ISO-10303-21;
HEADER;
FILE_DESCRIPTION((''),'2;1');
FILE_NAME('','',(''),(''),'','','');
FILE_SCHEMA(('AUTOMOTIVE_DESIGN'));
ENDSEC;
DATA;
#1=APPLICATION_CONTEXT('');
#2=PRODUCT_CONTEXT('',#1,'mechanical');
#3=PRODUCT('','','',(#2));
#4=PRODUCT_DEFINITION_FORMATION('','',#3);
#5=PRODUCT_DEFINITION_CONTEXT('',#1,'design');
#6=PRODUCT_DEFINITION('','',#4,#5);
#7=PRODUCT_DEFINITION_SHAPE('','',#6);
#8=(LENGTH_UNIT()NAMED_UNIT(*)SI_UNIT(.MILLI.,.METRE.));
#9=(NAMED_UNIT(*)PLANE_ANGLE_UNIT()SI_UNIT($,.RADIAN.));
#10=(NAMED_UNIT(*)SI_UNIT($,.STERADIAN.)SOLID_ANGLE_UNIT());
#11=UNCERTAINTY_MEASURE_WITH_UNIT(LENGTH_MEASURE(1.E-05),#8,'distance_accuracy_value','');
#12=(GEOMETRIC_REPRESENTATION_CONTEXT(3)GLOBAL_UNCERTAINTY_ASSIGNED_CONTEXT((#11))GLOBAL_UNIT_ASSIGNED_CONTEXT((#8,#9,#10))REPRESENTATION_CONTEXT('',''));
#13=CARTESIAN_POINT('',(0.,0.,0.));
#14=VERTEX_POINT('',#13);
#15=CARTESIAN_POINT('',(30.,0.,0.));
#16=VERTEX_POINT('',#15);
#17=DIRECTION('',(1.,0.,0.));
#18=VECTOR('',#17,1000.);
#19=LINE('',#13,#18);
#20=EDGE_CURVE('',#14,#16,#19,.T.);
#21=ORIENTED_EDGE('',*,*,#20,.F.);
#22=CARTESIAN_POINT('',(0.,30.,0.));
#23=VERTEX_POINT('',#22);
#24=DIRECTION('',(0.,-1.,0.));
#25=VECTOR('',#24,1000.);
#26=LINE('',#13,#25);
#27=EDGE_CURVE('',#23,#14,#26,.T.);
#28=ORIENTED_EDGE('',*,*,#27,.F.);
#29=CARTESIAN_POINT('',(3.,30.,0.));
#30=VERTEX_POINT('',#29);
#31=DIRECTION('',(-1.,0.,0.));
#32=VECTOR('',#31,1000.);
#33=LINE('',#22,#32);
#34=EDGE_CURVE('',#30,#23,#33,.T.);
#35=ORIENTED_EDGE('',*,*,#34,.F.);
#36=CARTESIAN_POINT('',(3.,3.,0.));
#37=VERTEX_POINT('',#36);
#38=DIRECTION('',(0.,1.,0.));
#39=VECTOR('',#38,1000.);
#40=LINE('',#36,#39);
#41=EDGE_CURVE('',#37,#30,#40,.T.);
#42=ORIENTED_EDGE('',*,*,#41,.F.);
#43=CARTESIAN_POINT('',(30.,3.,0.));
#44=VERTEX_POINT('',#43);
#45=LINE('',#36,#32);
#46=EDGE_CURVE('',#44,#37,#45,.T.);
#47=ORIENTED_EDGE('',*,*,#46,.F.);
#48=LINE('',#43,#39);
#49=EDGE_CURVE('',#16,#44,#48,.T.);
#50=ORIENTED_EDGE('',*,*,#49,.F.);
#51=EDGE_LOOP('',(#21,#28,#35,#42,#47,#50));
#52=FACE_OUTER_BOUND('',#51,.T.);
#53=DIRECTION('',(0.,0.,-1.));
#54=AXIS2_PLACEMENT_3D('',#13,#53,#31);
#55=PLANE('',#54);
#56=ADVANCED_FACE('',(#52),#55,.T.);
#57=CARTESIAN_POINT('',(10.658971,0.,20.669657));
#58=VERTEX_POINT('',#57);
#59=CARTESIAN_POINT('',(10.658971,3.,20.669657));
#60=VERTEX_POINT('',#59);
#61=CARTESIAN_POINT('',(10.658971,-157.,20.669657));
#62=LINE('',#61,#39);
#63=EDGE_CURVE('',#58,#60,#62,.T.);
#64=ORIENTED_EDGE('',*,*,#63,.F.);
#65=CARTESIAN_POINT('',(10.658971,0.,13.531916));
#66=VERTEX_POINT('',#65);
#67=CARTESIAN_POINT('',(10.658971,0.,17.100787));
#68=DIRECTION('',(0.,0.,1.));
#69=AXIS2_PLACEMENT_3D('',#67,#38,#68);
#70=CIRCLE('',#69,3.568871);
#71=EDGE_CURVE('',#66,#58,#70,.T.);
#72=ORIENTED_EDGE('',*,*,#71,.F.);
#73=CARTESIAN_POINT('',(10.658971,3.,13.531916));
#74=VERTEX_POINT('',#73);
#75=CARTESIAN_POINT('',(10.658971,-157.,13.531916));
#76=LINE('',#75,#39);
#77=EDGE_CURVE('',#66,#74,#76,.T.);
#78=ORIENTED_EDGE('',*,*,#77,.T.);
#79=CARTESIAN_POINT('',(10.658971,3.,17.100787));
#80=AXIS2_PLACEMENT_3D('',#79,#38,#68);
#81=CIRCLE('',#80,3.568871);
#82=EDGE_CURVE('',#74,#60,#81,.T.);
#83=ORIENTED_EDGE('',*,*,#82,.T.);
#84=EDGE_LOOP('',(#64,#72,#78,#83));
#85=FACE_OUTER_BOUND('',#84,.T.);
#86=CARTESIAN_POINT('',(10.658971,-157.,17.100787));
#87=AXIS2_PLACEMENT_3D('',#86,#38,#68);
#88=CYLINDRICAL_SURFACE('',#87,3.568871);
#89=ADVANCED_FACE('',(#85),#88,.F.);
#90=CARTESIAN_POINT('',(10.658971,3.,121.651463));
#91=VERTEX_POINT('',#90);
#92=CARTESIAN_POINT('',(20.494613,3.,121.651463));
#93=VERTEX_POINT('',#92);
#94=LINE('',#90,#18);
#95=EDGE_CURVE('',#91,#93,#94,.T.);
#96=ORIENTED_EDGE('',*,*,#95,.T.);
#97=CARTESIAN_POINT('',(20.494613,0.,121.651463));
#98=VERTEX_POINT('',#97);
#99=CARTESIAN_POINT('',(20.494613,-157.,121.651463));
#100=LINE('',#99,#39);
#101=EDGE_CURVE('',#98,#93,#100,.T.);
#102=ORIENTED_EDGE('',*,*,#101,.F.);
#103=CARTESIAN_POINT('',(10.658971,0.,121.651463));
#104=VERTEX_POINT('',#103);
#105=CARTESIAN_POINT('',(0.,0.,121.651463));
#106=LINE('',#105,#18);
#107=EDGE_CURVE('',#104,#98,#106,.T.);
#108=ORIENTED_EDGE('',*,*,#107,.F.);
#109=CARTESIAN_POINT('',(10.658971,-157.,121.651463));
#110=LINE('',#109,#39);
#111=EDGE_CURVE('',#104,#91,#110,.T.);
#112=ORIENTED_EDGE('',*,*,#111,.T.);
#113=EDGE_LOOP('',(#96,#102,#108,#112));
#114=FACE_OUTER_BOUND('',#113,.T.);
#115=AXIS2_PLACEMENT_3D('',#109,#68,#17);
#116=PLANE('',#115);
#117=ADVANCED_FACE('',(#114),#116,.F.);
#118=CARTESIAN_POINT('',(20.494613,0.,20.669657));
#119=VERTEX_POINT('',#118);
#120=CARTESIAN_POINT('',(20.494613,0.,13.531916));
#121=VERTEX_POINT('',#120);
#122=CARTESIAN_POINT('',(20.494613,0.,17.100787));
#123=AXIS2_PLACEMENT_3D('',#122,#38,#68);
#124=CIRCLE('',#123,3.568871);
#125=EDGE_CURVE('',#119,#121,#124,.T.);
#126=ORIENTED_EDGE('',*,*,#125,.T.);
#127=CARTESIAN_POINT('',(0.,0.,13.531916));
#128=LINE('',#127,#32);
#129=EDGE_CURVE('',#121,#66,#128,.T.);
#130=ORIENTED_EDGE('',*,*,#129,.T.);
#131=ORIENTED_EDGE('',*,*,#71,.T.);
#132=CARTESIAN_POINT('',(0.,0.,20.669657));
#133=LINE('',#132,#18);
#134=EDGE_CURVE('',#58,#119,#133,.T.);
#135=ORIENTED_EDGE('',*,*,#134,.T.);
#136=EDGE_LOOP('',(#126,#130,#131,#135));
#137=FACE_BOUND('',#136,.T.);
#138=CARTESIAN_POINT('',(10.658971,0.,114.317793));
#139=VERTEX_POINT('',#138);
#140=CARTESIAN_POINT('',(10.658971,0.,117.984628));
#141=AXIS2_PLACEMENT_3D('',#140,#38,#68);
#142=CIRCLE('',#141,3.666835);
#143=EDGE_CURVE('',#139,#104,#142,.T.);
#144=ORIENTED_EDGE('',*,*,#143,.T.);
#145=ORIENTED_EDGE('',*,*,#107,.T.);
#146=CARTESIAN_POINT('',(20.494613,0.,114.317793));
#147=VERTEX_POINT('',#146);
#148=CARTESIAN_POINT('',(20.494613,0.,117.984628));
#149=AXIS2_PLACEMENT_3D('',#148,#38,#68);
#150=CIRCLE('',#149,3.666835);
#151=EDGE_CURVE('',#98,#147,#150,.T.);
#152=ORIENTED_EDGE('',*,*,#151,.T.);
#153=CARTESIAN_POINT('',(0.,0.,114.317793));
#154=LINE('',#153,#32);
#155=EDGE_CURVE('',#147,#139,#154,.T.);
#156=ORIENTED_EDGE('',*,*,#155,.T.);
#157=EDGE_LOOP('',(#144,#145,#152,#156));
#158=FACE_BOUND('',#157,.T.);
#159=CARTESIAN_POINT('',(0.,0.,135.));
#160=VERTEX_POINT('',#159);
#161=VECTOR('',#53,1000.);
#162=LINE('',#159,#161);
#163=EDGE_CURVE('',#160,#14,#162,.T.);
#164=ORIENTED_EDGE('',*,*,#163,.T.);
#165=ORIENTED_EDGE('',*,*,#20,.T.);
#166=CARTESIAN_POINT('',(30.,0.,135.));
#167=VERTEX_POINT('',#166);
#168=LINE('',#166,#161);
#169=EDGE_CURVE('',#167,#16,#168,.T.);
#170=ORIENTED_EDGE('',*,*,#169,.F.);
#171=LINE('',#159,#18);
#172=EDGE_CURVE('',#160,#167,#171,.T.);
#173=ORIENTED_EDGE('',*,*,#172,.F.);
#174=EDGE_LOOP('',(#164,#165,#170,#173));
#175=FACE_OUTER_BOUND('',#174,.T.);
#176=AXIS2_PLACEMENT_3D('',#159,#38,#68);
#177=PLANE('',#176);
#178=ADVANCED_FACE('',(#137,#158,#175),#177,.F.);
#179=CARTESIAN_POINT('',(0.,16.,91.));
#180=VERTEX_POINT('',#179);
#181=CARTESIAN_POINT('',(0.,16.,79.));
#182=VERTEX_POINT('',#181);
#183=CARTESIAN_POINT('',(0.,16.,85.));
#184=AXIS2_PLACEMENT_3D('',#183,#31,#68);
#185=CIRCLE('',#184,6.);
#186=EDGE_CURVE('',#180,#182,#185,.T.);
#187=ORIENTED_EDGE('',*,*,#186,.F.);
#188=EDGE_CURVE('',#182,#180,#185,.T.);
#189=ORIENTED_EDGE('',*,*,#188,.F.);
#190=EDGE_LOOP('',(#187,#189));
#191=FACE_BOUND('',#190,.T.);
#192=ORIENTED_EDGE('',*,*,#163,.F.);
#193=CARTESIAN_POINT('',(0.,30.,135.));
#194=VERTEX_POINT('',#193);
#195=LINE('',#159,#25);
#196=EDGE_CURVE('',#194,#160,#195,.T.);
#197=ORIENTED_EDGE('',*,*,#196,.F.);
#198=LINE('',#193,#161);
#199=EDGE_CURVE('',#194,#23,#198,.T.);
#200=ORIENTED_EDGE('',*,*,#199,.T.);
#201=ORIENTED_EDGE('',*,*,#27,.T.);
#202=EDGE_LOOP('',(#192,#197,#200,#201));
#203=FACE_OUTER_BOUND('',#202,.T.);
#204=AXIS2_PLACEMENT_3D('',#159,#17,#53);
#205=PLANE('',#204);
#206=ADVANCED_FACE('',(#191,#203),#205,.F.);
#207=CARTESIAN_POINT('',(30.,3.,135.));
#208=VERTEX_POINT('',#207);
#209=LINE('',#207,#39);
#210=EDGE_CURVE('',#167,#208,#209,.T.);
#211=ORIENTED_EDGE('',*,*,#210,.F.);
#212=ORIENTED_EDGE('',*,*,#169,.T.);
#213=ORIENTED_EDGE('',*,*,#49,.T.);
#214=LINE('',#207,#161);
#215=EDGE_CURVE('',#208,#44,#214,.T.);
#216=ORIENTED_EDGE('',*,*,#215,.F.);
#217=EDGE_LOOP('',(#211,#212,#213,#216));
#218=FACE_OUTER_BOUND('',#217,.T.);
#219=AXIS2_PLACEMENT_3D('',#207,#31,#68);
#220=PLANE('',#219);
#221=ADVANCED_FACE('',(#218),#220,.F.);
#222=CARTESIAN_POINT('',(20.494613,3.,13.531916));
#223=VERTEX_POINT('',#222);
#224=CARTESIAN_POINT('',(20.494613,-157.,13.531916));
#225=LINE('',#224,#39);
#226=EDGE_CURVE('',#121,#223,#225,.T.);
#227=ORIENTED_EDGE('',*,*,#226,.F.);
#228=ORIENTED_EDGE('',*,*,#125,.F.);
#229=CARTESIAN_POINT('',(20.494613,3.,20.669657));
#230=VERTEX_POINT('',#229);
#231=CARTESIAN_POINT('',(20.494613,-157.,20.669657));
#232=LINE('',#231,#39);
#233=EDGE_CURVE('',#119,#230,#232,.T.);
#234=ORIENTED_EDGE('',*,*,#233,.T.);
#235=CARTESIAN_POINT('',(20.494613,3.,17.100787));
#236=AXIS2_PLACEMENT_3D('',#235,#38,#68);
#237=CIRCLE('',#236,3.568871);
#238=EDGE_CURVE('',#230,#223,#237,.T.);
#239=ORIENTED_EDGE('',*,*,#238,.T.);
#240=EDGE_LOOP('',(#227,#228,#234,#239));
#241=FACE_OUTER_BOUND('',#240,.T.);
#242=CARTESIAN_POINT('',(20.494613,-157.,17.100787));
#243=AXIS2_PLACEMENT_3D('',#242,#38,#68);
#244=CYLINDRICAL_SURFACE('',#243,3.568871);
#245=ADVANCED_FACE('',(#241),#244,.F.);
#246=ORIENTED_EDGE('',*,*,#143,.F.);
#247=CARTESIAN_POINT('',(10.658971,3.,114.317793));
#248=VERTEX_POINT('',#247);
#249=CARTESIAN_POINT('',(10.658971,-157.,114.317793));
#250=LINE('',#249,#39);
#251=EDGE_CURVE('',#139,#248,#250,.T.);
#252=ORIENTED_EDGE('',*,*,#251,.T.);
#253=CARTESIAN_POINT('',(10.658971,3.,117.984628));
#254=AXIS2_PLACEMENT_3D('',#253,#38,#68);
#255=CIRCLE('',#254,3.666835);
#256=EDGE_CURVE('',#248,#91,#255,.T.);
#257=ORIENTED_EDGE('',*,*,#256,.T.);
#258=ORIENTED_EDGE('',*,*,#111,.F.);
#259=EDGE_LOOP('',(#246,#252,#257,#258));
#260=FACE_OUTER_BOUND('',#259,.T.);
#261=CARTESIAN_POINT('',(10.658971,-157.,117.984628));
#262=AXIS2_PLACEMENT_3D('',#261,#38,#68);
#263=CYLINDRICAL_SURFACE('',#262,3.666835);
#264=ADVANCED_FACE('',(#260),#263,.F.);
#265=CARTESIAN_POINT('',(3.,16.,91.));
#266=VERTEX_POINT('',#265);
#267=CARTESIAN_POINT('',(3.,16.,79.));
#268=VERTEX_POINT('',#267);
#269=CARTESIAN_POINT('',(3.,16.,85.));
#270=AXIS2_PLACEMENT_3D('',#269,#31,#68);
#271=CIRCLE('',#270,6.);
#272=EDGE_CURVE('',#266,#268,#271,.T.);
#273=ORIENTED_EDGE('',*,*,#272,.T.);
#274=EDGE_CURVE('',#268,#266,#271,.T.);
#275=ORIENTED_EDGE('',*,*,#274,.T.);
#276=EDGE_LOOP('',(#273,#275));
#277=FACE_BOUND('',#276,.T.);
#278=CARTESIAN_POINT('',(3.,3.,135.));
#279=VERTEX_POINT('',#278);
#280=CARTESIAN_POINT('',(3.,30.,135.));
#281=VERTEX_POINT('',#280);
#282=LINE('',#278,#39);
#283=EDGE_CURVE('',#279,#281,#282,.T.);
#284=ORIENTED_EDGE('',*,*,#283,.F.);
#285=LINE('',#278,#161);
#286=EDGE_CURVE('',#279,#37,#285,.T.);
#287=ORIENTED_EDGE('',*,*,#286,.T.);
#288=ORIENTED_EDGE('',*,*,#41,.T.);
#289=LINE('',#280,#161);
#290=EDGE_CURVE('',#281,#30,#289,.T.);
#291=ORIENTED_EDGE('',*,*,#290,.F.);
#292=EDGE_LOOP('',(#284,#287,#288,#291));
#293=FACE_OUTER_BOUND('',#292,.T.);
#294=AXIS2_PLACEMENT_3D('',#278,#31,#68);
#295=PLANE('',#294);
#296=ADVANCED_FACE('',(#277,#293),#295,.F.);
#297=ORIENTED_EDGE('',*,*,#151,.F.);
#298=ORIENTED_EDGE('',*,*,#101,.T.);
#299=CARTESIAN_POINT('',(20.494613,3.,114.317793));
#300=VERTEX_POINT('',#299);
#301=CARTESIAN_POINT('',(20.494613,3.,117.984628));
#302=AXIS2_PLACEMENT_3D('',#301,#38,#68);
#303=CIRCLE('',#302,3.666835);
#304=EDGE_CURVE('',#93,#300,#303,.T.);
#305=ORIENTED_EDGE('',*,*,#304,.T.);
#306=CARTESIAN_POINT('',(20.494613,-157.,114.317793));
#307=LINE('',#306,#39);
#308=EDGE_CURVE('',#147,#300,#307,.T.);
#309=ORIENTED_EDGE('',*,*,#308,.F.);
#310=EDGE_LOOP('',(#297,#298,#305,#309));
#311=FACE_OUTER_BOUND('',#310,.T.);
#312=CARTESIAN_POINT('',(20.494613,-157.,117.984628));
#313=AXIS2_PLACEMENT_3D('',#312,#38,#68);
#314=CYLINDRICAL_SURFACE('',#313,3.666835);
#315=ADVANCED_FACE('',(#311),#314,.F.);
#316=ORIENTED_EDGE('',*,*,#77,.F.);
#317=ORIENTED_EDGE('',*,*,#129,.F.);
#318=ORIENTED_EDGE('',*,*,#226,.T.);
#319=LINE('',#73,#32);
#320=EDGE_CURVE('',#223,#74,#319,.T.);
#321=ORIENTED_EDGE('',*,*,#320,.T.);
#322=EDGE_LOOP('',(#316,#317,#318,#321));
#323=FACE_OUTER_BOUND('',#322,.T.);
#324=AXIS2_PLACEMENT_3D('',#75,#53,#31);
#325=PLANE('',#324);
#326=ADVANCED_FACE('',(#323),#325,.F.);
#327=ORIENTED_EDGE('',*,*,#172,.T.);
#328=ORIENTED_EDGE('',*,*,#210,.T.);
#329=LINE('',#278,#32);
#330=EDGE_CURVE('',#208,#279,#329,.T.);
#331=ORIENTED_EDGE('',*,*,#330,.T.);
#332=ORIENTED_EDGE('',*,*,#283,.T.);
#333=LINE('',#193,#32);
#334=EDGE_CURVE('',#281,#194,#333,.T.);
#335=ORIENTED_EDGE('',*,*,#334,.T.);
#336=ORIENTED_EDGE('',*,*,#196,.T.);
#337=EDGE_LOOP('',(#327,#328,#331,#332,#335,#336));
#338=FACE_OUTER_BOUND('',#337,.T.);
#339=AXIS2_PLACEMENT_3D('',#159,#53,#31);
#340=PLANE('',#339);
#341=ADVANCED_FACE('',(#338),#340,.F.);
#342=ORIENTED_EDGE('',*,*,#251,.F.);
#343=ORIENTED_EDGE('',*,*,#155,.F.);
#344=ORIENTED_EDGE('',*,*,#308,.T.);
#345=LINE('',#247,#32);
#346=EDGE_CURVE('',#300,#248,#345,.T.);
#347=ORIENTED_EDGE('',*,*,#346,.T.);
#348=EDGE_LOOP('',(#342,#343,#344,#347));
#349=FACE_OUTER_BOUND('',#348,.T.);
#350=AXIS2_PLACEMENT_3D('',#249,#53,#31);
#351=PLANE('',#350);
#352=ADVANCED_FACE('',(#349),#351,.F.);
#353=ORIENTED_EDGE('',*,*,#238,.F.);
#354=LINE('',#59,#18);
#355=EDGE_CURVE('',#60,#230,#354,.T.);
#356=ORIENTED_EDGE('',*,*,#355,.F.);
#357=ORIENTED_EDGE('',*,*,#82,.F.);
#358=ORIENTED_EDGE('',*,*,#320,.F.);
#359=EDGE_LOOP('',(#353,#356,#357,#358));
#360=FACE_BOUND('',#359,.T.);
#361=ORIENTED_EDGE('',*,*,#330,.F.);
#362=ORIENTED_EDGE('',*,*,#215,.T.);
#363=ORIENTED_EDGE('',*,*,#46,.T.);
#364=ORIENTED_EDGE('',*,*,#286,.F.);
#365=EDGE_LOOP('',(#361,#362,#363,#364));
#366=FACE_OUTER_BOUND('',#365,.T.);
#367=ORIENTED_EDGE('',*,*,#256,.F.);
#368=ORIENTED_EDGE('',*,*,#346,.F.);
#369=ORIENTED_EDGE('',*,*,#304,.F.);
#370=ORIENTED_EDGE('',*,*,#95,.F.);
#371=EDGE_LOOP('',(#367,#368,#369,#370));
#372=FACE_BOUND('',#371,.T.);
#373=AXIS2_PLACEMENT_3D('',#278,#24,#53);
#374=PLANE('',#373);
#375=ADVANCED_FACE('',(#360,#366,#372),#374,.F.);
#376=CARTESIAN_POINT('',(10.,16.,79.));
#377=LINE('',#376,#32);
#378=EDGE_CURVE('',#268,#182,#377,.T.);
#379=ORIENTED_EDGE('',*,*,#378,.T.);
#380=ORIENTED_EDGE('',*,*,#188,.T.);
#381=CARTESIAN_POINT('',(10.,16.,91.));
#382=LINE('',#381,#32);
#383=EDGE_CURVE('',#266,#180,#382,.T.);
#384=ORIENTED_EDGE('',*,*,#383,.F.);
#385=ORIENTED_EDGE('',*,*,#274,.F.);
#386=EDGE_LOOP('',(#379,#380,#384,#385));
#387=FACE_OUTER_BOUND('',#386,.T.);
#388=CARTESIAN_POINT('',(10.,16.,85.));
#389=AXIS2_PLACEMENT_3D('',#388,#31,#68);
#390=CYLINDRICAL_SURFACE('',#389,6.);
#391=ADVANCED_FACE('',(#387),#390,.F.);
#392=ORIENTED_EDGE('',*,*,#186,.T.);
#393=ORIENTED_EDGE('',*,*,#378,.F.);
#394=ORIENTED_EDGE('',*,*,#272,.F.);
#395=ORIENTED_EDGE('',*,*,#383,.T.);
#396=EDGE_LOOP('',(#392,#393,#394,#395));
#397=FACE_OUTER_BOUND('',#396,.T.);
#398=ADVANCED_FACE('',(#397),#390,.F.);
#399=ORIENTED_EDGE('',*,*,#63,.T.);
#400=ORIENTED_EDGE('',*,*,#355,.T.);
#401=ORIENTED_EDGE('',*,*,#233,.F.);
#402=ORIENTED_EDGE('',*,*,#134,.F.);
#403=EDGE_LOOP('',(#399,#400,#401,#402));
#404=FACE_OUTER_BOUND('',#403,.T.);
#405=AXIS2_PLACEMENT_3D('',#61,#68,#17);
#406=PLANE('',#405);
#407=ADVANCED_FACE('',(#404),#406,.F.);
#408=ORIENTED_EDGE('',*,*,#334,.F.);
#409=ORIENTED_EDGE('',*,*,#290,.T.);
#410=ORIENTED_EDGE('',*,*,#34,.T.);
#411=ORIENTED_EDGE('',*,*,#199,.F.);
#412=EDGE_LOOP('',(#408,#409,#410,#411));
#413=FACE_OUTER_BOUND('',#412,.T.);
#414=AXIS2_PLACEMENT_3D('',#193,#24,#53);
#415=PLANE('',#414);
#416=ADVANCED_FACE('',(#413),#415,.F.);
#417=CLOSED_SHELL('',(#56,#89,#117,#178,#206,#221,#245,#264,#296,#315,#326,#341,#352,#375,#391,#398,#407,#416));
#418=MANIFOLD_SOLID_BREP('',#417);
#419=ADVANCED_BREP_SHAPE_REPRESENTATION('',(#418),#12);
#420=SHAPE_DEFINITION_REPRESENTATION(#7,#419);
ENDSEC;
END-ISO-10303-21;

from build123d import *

# Parameters (mm, degrees)
BOSS_EXTRUDE1_DEPTH = 135
CUT_EXTRUDE1_DEPTH  = 160
SKETCH3_R           = 6
CUT_EXTRUDE2_DEPTH  = 10


with BuildPart() as part:
    # Sketch1 → Boss-Extrude1 (new body)
    with BuildSketch(Plane.XY):
        Polygon((0, 0), (0, 30), (3, 30), (3, 3), (30, 3), (30, 0), align=None)
    extrude(amount=BOSS_EXTRUDE1_DEPTH)

    # Sketch2 → Cut-Extrude1 (cut)
    with BuildSketch(Plane(origin=(0, 3, 0), x_dir=(1, 0, 0), z_dir=(0, 1, 0))):
        with BuildLine():
            Line((10.658971341, -13.531915857), (20.494612748, -13.531915857))
            ThreePointArc((20.494612748, -13.531915857), (24.063483391, -17.1007865), (20.494612748, -20.669657144))
            Line((20.494612748, -20.669657144), (10.658971341, -20.669657144))
            ThreePointArc((10.658971341, -20.669657144), (7.090100697, -17.1007865), (10.658971341, -13.531915857))
        make_face()
        with BuildLine():
            Line((10.658971341, -114.317792599), (20.494612748, -114.317792599))
            ThreePointArc((20.494612748, -114.317792599), (24.161447744, -117.984627595), (20.494612748, -121.65146259))
            Line((20.494612748, -121.65146259), (10.658971341, -121.65146259))
            ThreePointArc((10.658971341, -121.65146259), (6.992136345, -117.984627595), (10.658971341, -114.317792599))
        make_face()
    extrude(amount=-CUT_EXTRUDE1_DEPTH, mode=Mode.SUBTRACT)

    # Sketch3 → Cut-Extrude2 (cut)
    with BuildSketch(Plane.ZY):
        with Locations((85, 16)):
            Circle(SKETCH3_R)
    extrude(amount=-CUT_EXTRUDE2_DEPTH, mode=Mode.SUBTRACT)


solid = part.part
